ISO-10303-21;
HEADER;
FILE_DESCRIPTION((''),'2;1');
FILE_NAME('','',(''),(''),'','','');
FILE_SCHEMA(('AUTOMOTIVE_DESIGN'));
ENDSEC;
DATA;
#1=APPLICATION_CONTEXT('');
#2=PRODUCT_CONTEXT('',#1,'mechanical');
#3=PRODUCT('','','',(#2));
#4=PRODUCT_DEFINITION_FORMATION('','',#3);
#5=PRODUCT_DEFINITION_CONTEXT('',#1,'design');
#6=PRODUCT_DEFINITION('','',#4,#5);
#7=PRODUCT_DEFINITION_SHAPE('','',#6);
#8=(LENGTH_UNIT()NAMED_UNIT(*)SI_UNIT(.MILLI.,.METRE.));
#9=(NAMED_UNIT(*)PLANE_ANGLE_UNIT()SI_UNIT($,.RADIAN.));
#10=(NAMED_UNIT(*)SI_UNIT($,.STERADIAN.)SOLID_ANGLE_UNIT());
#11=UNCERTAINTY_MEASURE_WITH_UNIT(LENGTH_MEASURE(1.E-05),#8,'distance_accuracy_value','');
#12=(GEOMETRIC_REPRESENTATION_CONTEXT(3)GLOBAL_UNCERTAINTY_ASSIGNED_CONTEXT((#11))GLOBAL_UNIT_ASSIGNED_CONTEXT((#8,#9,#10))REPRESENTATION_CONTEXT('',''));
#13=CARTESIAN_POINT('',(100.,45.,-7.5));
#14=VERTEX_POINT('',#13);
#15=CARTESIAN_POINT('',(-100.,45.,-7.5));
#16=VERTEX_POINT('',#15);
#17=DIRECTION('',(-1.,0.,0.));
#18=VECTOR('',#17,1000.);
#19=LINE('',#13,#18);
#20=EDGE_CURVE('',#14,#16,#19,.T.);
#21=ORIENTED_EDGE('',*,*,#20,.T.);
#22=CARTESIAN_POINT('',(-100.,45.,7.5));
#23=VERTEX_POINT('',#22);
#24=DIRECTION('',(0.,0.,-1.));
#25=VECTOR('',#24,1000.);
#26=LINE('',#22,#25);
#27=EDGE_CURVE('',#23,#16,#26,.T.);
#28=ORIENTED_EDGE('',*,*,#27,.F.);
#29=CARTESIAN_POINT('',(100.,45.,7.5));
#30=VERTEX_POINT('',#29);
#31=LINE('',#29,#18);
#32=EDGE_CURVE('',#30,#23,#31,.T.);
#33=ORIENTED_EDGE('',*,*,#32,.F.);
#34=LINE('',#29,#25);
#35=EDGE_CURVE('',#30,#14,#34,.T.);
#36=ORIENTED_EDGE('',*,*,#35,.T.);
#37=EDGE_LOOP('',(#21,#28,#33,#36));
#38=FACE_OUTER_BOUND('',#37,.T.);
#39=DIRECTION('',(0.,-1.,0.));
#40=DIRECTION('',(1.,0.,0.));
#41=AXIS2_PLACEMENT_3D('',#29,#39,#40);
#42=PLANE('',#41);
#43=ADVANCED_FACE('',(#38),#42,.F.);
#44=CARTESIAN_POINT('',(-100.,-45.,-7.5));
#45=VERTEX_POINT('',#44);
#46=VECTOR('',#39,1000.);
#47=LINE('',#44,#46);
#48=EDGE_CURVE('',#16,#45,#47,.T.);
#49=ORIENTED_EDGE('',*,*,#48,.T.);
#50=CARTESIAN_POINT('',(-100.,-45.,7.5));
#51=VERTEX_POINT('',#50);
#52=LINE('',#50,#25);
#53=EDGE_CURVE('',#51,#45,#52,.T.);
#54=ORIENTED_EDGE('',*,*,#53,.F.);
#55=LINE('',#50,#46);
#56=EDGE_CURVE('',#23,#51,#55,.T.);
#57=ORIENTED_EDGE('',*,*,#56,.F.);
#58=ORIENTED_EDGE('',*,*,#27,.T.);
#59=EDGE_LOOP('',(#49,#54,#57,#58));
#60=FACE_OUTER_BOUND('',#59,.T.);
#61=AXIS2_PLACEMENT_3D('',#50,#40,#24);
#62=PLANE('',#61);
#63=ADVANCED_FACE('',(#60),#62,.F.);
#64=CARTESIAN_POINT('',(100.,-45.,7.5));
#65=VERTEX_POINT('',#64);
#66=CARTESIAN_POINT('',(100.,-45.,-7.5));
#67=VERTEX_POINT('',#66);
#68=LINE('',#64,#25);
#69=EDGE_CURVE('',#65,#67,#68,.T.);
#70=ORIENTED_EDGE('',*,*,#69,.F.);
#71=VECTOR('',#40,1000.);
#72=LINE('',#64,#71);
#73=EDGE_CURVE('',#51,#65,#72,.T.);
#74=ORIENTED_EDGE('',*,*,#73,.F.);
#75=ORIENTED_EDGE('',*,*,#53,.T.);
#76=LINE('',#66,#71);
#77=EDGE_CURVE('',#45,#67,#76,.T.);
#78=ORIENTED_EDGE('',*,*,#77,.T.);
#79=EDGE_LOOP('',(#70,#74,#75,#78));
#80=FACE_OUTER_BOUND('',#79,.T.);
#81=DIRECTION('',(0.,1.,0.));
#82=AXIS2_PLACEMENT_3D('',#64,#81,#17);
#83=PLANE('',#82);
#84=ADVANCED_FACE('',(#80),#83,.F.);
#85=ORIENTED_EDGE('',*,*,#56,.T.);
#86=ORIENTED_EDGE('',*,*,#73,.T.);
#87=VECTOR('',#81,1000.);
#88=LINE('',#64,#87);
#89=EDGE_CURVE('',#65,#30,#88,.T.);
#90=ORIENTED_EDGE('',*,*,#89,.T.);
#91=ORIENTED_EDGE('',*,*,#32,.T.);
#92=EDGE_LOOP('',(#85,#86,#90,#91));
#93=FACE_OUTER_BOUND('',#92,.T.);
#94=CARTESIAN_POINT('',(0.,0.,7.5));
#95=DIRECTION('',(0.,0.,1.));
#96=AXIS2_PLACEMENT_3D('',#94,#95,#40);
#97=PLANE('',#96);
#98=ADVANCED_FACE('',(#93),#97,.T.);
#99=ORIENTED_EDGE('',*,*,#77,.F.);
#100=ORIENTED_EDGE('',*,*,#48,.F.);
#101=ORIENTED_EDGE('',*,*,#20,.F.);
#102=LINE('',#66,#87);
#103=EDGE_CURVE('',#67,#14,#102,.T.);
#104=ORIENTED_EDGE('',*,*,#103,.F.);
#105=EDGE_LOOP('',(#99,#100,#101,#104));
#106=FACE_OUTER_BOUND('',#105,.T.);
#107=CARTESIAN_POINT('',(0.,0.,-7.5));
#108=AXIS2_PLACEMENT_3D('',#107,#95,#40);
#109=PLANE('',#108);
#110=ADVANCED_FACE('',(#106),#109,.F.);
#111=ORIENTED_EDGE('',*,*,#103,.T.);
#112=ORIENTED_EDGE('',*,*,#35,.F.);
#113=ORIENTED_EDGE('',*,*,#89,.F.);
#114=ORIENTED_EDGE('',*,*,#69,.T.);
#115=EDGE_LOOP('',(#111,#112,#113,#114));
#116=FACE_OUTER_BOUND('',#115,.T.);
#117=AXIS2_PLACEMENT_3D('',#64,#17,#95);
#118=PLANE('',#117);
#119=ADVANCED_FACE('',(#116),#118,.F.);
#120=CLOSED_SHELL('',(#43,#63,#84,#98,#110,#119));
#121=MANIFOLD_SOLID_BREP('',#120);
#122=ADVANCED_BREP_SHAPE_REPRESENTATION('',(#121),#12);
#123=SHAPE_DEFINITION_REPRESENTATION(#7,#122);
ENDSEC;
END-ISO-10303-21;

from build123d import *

# Parameters (mm, degrees)
SKETCH1_W           = 200
SKETCH1_H           = 90
BOSS_EXTRUDE1_DEPTH = 7.5


with BuildPart() as part:
    # Sketch1 → Boss-Extrude1 (new, symmetric)
    with BuildSketch(Plane.XY):
        Rectangle(SKETCH1_W, SKETCH1_H)
    extrude(amount=BOSS_EXTRUDE1_DEPTH, both=True)


solid = part.part
